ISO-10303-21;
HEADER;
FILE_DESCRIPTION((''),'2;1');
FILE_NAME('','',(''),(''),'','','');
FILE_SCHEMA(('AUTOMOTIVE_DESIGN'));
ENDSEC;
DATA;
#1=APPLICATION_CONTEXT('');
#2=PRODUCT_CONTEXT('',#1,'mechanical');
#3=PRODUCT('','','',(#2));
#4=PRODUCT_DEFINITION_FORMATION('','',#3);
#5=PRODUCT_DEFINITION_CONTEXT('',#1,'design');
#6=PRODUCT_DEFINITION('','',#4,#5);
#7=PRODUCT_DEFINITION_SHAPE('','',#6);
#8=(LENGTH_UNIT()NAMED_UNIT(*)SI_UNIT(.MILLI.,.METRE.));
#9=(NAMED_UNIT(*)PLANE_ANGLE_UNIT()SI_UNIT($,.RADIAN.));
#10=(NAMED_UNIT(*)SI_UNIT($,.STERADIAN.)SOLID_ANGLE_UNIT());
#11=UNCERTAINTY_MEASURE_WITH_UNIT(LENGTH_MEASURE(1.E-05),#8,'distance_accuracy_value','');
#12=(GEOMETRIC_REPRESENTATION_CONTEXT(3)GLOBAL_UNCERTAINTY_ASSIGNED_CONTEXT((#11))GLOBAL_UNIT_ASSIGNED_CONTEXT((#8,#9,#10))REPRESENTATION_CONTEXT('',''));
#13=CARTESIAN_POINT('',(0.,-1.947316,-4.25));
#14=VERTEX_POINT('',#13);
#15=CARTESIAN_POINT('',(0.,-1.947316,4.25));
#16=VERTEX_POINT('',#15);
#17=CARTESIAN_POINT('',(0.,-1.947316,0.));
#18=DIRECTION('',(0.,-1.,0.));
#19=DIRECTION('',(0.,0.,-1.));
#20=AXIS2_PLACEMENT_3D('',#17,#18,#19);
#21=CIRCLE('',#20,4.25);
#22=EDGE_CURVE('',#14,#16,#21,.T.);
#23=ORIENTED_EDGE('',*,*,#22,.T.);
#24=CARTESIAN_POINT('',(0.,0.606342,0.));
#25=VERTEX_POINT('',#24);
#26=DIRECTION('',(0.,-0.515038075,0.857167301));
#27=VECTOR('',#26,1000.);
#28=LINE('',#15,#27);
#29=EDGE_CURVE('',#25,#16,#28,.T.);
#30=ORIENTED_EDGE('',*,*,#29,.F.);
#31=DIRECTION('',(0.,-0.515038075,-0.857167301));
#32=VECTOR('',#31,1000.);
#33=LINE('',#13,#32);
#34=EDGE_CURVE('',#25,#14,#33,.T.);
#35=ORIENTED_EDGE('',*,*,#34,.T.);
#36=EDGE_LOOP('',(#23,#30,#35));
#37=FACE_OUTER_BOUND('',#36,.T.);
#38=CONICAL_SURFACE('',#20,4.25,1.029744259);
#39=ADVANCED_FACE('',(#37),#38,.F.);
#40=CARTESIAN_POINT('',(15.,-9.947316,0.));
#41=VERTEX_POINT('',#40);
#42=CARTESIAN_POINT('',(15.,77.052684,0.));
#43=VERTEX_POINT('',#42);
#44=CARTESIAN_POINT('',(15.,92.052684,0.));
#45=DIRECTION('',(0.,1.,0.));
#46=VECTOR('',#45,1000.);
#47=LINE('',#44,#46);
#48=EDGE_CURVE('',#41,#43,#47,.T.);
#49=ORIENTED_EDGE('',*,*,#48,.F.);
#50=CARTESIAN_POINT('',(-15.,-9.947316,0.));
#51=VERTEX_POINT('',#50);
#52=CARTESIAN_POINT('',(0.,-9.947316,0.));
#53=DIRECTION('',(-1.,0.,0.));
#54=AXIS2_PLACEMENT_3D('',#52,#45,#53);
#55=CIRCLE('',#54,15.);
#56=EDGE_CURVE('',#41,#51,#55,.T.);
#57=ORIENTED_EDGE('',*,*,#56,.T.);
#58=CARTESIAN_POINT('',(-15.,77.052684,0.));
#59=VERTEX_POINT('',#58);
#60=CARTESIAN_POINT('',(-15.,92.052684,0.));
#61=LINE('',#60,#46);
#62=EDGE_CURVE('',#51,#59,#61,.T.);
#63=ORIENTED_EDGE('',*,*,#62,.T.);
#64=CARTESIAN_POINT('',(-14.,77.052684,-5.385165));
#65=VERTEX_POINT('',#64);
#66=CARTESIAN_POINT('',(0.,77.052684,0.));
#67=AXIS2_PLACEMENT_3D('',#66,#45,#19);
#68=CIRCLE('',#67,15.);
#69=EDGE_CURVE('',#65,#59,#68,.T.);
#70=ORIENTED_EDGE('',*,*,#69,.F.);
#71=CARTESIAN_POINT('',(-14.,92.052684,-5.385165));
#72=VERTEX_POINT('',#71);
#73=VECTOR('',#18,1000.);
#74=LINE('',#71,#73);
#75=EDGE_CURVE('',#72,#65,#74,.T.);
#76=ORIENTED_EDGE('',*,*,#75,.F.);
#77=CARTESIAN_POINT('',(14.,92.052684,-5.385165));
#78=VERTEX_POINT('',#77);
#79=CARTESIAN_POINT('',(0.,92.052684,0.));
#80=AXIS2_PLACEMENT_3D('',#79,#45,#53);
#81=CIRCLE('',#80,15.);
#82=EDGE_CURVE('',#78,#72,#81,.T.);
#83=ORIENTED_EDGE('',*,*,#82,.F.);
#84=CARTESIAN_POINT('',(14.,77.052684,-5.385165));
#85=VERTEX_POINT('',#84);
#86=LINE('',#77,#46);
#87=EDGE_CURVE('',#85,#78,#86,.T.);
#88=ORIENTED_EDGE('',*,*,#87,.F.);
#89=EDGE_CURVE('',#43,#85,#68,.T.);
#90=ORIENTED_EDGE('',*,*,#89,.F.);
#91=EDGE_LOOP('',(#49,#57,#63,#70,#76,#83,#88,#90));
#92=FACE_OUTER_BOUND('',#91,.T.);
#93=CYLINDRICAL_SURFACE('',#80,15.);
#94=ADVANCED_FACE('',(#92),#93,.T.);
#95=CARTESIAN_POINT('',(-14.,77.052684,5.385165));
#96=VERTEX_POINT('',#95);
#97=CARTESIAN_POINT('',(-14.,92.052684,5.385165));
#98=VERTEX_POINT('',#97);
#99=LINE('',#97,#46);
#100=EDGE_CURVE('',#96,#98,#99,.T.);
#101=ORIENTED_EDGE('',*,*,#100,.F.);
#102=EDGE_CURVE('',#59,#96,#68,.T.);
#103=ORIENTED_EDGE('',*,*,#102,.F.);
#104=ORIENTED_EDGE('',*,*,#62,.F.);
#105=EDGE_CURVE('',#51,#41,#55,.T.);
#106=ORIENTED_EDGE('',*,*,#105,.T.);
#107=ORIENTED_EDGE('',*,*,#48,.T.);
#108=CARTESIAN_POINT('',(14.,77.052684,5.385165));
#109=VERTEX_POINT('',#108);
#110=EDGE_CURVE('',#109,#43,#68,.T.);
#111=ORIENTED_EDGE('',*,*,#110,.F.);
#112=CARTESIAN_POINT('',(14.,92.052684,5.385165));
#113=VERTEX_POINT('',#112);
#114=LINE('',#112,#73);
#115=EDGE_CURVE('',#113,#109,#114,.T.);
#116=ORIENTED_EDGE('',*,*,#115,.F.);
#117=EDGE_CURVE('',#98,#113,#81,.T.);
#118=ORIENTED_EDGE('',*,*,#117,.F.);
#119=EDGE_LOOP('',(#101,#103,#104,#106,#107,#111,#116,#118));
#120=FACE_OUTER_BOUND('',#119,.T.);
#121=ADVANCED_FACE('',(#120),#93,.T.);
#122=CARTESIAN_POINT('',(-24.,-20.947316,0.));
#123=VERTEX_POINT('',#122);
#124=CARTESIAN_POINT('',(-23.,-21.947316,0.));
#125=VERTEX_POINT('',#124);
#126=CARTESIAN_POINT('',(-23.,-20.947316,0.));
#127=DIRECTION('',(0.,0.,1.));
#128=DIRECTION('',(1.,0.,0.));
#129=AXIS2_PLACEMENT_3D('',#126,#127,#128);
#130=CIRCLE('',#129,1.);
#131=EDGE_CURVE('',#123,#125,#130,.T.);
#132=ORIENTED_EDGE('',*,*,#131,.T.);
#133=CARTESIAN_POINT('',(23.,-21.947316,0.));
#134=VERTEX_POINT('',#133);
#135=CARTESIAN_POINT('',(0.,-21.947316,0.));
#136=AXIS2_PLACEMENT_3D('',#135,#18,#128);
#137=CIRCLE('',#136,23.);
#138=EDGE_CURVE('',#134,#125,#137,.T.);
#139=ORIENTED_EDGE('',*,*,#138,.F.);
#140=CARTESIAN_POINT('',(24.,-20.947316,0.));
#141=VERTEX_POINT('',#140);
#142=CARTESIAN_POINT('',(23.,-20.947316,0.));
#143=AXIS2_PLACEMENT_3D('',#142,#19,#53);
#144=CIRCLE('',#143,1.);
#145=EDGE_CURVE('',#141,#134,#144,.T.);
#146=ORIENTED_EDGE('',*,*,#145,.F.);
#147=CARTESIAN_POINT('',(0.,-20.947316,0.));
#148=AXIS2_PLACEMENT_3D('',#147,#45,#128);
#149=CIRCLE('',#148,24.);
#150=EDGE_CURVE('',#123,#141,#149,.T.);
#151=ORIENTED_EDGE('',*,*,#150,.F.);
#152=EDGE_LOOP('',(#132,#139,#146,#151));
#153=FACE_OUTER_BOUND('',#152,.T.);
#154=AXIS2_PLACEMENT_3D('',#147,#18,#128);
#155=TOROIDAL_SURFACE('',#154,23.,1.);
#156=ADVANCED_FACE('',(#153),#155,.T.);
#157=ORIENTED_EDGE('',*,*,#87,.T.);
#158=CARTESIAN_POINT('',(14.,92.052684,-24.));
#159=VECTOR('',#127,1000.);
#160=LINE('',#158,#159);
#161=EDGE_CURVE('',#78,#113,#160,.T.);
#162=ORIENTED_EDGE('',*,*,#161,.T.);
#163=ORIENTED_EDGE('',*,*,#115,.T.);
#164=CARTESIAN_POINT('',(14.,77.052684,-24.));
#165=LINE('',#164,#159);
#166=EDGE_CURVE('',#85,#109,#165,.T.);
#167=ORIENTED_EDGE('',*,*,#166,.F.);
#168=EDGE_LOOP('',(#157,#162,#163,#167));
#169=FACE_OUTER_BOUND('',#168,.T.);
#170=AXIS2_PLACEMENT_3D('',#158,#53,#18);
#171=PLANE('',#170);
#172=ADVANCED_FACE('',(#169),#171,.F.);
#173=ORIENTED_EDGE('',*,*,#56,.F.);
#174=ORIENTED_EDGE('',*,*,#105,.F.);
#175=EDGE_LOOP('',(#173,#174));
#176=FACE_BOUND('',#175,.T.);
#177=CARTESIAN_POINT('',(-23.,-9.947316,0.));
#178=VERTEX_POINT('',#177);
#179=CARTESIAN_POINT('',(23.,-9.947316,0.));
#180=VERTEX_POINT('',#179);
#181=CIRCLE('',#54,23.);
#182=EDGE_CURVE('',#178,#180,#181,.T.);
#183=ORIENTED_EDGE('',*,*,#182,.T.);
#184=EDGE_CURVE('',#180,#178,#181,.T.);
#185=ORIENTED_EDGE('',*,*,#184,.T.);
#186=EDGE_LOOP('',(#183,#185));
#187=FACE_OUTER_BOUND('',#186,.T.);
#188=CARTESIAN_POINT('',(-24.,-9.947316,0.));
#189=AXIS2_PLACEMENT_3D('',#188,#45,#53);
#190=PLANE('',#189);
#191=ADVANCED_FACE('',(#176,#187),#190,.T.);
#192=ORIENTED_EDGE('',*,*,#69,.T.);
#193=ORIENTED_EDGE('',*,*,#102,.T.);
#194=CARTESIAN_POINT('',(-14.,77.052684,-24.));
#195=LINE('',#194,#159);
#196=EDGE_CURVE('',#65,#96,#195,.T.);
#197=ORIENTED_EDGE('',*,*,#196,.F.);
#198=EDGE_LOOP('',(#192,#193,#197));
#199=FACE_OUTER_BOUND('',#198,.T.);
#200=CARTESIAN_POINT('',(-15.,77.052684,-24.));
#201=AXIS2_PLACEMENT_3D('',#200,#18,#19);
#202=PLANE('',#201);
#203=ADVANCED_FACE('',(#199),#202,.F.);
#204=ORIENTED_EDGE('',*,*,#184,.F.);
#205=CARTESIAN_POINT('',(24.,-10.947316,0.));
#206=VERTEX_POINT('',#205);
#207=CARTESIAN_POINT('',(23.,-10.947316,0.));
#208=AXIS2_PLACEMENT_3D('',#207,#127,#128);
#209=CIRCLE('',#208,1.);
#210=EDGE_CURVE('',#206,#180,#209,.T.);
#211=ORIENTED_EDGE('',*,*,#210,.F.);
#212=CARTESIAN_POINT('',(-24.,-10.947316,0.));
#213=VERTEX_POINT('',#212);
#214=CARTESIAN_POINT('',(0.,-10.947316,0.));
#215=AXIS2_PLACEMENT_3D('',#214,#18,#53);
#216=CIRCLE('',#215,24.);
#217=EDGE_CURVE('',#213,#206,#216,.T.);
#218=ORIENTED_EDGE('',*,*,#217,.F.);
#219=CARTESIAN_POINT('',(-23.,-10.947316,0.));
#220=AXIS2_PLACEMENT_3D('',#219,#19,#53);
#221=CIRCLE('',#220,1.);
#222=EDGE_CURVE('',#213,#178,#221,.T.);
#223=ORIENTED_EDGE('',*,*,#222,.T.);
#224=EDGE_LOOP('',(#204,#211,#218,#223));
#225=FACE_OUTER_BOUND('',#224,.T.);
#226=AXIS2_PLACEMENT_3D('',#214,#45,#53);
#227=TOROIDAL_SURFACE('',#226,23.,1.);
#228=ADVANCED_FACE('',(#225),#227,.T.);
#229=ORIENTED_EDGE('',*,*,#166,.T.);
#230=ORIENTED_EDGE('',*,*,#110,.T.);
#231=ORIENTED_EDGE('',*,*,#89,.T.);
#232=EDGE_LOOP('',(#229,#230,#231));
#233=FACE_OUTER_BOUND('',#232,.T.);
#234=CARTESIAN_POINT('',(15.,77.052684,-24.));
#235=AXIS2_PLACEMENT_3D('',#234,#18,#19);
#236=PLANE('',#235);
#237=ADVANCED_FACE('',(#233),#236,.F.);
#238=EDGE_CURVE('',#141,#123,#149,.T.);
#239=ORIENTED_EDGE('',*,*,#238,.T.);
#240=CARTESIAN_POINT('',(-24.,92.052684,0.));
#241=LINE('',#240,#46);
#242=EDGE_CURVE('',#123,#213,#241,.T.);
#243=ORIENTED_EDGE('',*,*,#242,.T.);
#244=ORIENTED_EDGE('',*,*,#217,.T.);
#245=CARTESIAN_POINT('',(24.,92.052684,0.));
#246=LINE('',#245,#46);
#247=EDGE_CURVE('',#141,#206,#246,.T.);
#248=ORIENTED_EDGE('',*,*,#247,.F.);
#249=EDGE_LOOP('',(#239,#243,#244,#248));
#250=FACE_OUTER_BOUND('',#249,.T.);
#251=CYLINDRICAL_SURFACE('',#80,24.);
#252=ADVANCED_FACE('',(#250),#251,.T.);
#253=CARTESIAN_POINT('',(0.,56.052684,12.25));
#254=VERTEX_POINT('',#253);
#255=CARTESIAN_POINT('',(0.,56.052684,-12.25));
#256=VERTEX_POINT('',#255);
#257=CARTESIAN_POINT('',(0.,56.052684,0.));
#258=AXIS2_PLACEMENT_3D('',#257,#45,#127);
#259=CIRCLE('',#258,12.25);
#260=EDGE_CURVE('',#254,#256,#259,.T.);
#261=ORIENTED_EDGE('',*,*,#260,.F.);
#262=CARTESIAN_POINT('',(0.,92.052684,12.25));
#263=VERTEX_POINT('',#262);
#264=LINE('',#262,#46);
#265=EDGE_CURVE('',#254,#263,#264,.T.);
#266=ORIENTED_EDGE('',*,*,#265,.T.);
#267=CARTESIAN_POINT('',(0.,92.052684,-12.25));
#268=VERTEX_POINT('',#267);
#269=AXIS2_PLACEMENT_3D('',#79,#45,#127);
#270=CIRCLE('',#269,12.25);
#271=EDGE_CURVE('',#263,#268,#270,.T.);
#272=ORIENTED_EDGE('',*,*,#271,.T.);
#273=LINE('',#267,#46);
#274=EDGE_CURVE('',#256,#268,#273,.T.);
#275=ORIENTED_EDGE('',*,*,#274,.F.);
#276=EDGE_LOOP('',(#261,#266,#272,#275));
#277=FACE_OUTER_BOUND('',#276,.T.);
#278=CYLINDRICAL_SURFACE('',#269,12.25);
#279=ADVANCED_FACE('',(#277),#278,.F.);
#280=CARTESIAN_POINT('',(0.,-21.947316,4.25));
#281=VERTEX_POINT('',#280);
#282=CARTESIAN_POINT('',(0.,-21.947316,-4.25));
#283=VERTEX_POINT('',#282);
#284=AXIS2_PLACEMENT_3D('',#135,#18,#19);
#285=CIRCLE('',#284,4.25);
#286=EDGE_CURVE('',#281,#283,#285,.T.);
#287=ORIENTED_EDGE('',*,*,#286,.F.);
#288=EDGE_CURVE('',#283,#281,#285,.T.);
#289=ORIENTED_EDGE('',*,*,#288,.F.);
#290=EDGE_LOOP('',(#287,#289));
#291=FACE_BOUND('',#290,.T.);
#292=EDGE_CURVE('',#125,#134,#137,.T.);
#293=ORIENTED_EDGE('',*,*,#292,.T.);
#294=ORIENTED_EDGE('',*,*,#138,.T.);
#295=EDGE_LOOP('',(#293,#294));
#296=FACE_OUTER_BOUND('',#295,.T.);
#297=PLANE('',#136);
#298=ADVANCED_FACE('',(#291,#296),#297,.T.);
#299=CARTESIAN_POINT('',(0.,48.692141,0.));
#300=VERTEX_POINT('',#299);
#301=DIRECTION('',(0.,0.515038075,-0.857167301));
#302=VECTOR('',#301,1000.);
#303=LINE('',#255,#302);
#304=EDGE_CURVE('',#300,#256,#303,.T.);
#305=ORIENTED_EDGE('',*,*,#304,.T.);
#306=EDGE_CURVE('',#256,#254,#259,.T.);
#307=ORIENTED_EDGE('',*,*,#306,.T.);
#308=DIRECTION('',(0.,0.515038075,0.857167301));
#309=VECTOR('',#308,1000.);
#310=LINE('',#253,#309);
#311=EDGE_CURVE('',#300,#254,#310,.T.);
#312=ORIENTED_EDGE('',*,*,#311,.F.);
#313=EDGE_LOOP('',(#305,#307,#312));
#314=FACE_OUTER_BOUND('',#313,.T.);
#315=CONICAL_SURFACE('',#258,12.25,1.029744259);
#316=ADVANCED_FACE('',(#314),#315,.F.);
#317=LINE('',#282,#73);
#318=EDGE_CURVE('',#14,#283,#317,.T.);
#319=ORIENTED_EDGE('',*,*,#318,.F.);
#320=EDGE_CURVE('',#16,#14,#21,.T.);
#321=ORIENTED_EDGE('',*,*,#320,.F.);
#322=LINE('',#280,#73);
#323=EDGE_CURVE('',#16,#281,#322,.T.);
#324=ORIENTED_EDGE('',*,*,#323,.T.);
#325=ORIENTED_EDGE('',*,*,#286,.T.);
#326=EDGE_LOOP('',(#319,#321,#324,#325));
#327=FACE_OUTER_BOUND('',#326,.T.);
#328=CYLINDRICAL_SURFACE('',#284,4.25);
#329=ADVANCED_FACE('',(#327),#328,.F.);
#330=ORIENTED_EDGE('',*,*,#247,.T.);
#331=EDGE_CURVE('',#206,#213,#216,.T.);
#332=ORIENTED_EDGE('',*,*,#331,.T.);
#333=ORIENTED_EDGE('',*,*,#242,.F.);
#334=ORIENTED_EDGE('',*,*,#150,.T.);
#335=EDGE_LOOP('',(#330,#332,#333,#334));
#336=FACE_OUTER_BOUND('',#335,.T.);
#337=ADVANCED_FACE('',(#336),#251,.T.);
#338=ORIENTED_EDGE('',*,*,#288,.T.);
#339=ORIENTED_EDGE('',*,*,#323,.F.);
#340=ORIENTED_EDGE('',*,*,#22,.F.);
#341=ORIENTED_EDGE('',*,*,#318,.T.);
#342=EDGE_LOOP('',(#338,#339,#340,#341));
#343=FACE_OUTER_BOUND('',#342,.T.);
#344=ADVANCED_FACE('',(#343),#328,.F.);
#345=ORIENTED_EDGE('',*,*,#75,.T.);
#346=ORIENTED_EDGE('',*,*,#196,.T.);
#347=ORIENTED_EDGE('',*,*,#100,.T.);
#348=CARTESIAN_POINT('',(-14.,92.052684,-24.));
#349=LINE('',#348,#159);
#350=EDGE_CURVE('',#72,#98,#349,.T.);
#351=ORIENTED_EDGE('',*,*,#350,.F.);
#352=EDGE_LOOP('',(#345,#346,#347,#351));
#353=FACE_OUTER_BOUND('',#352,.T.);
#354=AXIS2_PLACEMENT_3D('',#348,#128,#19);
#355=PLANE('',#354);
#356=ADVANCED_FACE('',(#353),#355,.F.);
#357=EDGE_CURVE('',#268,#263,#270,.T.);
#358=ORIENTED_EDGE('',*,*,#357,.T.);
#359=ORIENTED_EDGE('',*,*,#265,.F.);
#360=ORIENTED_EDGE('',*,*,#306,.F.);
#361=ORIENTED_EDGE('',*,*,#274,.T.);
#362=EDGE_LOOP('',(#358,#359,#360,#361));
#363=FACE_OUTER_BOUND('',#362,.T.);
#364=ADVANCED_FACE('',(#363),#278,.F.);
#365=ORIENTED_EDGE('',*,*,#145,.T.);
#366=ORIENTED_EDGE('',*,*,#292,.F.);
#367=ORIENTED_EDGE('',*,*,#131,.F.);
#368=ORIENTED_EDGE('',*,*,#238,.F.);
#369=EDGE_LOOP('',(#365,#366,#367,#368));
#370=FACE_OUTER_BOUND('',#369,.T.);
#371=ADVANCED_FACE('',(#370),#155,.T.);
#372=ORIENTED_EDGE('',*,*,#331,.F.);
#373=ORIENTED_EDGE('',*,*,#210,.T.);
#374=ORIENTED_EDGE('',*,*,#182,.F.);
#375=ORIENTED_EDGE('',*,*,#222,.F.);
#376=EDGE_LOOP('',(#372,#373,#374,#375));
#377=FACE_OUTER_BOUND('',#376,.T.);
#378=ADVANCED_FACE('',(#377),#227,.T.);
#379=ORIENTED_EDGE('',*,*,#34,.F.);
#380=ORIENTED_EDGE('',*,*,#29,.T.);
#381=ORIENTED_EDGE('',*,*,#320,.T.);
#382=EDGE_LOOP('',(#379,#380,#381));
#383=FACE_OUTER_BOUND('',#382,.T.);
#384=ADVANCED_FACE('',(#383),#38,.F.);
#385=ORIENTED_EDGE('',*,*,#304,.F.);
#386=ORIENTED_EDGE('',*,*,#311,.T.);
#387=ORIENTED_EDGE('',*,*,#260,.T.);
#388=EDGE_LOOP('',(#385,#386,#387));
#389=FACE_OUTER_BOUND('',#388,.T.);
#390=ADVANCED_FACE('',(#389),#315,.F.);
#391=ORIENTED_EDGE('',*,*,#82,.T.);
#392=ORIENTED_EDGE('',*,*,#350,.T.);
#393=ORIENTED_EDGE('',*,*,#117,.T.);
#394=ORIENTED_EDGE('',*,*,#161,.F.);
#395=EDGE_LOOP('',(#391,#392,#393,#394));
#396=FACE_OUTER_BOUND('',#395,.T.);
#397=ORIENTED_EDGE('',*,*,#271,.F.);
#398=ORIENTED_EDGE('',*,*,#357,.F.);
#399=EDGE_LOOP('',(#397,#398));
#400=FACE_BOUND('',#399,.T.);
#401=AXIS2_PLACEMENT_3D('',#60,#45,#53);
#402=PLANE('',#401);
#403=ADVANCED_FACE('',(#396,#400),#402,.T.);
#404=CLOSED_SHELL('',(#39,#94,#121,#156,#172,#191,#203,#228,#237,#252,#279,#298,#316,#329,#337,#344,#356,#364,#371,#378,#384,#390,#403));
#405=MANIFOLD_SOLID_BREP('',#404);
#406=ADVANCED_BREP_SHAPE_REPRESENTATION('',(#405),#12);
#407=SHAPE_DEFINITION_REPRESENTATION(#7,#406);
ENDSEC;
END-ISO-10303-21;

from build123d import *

# Parameters (mm, degrees)
CUT_EXTRUDE1_DEPTH      = 99.11063461
CUT_EXTRUDE1_DEPTH_BACK = 99.11063461
SKETCH2_W               = 1
SKETCH2_H               = 15
FILLET1_R               = 1
M27_TAPPED_HOLE1_D      = 24.5
M27_TAPPED_HOLE1_DEPTH  = 36
M27_TAPPED_HOLE1_TIP    = 7.360542583
M10_TAPPED_HOLE1_D      = 8.5
M10_TAPPED_HOLE1_DEPTH  = 20
M10_TAPPED_HOLE1_TIP    = 2.553657631


with BuildPart() as part:
    # Sketch1 → Revolve1 (revolve)
    with BuildSketch(Plane.XY):
        Polygon((0, 92.052683956), (0, -21.947316044), (-24, -21.947316044), (-24, -9.947316044), (-15, -9.947316044), (-15, 92.052683956), align=None)
    revolve(axis=Axis((0, 92.052683956, 0), (0, -1, 0)))

    # Sketch2 → Cut-Extrude1 (cut, two sides: drawn at the far end of the back side and taken through both)
    with BuildSketch(Plane.XY.offset(-CUT_EXTRUDE1_DEPTH_BACK)):
        with Locations((14.5, 84.552683956)):
            Rectangle(SKETCH2_W, SKETCH2_H)
        with Locations((-14.5, 84.552683956)):
            Rectangle(SKETCH2_W, SKETCH2_H)
    extrude(amount=CUT_EXTRUDE1_DEPTH + CUT_EXTRUDE1_DEPTH_BACK, mode=Mode.SUBTRACT)

    # Fillet1
    fillet1_edges = [part.edges().sort_by_distance(p)[0] for p in [
        (24, -9.947316044, 0),
        (24, -21.947316044, 0),
    ]]
    fillet(fillet1_edges, radius=FILLET1_R)

    # M27 Tapped Hole1
    with Locations(Plane(origin=(0, 92.052683956, 0), x_dir=(1, 0, 0), z_dir=(0, 1, 0))):
        with Locations((0, 0)):
            Hole(M27_TAPPED_HOLE1_D / 2, depth=M27_TAPPED_HOLE1_DEPTH)
            with Locations((0, 0, -(M27_TAPPED_HOLE1_DEPTH + M27_TAPPED_HOLE1_TIP / 2))):  # 118° drill point
                Cone(0, M27_TAPPED_HOLE1_D / 2, M27_TAPPED_HOLE1_TIP, mode=Mode.SUBTRACT)

    # M10 Tapped Hole1
    with Locations(Plane(origin=(0, -21.947316044, 0), x_dir=(-1, 0, 0), z_dir=(0, -1, 0))):
        with Locations((0, 0)):
            Hole(M10_TAPPED_HOLE1_D / 2, depth=M10_TAPPED_HOLE1_DEPTH)
            with Locations((0, 0, -(M10_TAPPED_HOLE1_DEPTH + M10_TAPPED_HOLE1_TIP / 2))):  # 118° drill point
                Cone(0, M10_TAPPED_HOLE1_D / 2, M10_TAPPED_HOLE1_TIP, mode=Mode.SUBTRACT)


solid = part.part
